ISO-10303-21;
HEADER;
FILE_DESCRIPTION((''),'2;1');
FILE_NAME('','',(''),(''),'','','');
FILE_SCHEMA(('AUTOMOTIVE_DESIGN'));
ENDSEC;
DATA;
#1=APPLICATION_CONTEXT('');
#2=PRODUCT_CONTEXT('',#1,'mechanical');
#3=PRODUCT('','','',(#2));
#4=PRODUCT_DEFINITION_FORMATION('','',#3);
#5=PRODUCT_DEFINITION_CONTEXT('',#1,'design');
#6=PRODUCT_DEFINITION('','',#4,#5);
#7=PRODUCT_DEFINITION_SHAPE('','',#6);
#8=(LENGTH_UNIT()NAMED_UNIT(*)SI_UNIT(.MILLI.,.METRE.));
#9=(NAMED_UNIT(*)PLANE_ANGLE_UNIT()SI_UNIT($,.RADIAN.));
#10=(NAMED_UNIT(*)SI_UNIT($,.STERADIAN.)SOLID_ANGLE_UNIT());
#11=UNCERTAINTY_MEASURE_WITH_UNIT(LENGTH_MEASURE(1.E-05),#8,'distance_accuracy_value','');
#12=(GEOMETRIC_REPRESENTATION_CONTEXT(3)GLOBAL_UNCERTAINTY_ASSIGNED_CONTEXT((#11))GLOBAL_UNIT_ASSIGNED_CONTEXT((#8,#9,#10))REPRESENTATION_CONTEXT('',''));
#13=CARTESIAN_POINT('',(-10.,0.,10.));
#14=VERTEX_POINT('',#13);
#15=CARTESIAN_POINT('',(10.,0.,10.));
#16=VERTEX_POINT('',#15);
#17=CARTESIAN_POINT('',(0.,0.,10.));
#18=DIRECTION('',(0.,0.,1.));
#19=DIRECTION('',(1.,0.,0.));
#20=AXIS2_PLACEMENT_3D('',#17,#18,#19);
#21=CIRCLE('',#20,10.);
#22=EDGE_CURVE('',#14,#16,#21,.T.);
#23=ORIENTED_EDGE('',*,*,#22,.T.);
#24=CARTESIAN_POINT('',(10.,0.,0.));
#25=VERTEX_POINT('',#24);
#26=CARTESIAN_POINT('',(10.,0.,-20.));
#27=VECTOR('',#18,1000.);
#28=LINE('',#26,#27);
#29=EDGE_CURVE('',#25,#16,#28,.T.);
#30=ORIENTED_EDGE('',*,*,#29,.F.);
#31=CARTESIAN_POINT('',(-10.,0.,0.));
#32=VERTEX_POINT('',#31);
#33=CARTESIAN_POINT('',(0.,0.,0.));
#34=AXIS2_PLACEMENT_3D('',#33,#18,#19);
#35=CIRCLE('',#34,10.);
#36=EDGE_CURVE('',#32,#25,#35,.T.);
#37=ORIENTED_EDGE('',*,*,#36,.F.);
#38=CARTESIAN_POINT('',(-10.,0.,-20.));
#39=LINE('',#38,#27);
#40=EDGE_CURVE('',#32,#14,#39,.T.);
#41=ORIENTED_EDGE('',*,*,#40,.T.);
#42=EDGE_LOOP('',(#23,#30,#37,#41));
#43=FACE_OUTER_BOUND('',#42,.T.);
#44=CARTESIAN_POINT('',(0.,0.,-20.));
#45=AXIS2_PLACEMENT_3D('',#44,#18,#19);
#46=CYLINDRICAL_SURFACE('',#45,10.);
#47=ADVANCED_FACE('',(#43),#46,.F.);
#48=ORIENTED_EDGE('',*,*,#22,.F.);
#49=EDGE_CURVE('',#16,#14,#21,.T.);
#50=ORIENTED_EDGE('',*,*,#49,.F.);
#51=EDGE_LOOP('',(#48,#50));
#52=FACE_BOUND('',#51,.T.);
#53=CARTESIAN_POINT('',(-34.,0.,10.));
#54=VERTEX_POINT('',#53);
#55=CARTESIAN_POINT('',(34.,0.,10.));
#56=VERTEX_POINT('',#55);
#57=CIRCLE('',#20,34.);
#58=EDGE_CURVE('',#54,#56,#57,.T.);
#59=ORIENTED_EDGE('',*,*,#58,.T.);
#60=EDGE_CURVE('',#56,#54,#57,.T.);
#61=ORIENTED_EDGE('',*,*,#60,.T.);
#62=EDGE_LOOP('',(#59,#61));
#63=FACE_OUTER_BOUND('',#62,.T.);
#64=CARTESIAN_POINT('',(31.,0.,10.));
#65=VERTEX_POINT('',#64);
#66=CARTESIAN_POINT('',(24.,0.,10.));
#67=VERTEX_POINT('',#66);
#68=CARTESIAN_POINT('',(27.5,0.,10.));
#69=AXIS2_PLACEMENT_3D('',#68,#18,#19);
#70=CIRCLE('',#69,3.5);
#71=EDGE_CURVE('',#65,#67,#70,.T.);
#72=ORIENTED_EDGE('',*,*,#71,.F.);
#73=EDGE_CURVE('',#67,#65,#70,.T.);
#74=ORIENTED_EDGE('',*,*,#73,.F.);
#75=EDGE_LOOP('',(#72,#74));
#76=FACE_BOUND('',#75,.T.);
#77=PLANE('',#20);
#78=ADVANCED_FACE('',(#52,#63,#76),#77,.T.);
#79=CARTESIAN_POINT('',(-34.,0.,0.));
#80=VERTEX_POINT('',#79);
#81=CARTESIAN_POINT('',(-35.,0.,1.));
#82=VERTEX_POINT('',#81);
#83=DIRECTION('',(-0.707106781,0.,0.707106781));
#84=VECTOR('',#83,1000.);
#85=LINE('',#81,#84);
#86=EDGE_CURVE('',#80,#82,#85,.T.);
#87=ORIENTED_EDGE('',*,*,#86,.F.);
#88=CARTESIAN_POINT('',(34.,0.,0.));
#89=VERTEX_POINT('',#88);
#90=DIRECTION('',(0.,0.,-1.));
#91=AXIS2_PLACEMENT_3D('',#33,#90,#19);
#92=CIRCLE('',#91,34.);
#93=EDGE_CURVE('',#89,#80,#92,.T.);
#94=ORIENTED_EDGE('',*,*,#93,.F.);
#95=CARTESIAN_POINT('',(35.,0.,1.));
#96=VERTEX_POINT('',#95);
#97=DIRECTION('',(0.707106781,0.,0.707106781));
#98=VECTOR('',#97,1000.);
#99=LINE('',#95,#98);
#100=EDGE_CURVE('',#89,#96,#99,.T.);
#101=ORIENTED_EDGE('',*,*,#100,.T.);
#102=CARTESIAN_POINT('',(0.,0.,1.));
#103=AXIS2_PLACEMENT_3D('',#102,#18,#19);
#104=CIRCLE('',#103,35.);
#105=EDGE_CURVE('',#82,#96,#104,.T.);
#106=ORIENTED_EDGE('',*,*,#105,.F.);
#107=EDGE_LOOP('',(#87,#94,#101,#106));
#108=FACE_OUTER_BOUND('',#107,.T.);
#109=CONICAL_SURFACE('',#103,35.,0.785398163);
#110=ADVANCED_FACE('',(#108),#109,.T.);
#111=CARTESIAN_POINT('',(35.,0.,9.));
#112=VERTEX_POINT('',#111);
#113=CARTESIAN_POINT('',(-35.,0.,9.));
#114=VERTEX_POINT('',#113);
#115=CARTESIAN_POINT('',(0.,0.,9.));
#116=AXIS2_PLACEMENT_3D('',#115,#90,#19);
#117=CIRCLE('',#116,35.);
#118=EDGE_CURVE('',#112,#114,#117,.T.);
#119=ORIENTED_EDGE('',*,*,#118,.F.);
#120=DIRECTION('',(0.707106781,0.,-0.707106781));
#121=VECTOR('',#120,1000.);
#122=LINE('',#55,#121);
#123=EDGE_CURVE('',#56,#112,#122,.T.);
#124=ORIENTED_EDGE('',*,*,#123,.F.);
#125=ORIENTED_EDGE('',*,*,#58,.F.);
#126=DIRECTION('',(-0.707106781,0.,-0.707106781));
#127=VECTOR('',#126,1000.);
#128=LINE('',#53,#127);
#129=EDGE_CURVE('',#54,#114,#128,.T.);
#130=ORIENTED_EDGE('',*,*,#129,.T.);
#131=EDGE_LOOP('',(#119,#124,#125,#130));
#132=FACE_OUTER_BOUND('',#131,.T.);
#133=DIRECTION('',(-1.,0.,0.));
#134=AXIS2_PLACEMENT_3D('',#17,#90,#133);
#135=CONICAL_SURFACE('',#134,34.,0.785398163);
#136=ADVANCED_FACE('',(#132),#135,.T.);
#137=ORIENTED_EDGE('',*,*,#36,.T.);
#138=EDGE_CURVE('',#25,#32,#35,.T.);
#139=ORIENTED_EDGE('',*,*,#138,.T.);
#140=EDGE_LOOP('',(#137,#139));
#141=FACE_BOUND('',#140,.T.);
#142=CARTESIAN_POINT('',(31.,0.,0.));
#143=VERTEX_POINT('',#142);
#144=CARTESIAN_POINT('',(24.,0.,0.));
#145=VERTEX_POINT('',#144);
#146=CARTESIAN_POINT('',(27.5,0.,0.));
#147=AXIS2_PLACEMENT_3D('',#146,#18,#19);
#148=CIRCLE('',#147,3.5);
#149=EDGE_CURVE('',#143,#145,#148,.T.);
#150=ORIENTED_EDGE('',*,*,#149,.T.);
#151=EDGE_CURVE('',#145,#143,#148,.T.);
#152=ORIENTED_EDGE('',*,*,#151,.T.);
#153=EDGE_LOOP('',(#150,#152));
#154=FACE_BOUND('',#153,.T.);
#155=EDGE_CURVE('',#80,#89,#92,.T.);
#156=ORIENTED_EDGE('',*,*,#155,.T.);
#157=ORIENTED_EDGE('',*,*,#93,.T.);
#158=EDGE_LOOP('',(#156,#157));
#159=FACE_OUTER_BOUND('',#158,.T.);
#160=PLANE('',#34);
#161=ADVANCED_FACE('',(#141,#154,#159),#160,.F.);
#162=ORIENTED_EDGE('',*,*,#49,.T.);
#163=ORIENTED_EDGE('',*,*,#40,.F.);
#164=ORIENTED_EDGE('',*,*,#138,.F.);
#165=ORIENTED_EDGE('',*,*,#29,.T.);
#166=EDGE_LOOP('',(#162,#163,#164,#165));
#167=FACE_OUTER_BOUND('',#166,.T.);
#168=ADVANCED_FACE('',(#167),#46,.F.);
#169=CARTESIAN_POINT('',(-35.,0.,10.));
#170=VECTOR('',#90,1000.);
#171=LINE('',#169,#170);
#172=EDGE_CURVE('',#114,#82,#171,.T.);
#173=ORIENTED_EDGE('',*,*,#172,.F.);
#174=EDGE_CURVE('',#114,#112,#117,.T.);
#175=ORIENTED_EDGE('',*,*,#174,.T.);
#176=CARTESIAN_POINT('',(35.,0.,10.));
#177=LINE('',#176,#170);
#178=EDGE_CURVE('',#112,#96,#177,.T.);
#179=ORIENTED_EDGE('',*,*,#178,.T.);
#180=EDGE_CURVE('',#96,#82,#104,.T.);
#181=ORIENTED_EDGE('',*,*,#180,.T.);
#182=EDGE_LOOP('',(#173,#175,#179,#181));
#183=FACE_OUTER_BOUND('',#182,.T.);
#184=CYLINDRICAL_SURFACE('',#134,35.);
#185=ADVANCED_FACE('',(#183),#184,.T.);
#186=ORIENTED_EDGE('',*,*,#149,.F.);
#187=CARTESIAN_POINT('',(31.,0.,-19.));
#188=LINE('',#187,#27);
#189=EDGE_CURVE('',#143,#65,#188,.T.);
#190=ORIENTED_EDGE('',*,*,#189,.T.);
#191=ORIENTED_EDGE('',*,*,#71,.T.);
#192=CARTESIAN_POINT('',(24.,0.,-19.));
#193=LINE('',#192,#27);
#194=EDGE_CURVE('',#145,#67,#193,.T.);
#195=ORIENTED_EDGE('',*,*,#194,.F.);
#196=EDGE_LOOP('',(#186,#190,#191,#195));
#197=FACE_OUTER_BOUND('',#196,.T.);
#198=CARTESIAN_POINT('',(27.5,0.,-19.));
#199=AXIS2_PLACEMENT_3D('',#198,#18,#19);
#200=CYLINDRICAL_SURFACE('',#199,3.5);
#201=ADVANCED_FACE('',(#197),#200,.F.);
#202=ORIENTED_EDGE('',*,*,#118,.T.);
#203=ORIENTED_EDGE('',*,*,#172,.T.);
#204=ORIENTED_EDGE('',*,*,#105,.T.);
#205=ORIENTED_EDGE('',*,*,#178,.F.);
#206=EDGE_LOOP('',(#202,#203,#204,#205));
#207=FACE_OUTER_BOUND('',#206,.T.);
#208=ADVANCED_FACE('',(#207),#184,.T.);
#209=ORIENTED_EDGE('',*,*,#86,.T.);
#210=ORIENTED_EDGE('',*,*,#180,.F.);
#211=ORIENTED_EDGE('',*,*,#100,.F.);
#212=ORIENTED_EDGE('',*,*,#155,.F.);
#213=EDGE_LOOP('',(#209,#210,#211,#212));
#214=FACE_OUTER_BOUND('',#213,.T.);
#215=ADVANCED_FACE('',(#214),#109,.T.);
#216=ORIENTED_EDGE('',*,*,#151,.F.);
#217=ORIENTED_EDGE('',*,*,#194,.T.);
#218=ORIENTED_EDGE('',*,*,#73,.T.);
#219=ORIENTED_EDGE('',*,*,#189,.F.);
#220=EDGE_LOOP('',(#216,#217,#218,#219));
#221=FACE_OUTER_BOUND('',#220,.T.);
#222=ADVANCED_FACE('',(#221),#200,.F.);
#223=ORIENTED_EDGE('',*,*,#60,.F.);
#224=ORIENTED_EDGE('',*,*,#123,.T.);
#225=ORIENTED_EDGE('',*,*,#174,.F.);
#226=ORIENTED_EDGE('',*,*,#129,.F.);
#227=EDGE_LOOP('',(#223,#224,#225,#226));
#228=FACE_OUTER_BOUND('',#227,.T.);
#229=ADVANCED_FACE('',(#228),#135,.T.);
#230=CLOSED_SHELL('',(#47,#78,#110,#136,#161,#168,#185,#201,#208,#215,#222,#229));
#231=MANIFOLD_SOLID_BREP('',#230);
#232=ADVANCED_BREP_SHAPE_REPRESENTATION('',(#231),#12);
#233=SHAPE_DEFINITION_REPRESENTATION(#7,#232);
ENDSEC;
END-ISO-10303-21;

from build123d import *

# Parameters (mm, degrees)
SKETCH1_R           = 35
BOSS_EXTRUDE1_DEPTH = 10
CHAMFER1_SIZE       = 1
SKETCH2_R           = 10
CUT_EXTRUDE1_DEPTH  = 30
SKETCH3_R           = 3.5
CUT_EXTRUDE2_DEPTH  = 29


with BuildPart() as part:
    # Sketch1 → Boss-Extrude1 (new body)
    with BuildSketch(Plane.XY):
        Circle(SKETCH1_R)
    extrude(amount=BOSS_EXTRUDE1_DEPTH)

    # Chamfer1
    chamfer1_edges = [part.edges().sort_by_distance(p)[0] for p in [
        (-35, 0, 0),
        (-35, 0, 10),
    ]]
    chamfer(chamfer1_edges, length=CHAMFER1_SIZE)

    # Sketch2 → Cut-Extrude1 (cut)
    with BuildSketch(Plane.XY.offset(10)):
        Circle(SKETCH2_R)
    extrude(amount=-CUT_EXTRUDE1_DEPTH, mode=Mode.SUBTRACT)

    # Sketch3 → Cut-Extrude2 (cut)
    with BuildSketch(Plane.XY.offset(10)):
        with Locations((27.5, 0)):
            Circle(SKETCH3_R)
    extrude(amount=-CUT_EXTRUDE2_DEPTH, mode=Mode.SUBTRACT)


solid = part.part
